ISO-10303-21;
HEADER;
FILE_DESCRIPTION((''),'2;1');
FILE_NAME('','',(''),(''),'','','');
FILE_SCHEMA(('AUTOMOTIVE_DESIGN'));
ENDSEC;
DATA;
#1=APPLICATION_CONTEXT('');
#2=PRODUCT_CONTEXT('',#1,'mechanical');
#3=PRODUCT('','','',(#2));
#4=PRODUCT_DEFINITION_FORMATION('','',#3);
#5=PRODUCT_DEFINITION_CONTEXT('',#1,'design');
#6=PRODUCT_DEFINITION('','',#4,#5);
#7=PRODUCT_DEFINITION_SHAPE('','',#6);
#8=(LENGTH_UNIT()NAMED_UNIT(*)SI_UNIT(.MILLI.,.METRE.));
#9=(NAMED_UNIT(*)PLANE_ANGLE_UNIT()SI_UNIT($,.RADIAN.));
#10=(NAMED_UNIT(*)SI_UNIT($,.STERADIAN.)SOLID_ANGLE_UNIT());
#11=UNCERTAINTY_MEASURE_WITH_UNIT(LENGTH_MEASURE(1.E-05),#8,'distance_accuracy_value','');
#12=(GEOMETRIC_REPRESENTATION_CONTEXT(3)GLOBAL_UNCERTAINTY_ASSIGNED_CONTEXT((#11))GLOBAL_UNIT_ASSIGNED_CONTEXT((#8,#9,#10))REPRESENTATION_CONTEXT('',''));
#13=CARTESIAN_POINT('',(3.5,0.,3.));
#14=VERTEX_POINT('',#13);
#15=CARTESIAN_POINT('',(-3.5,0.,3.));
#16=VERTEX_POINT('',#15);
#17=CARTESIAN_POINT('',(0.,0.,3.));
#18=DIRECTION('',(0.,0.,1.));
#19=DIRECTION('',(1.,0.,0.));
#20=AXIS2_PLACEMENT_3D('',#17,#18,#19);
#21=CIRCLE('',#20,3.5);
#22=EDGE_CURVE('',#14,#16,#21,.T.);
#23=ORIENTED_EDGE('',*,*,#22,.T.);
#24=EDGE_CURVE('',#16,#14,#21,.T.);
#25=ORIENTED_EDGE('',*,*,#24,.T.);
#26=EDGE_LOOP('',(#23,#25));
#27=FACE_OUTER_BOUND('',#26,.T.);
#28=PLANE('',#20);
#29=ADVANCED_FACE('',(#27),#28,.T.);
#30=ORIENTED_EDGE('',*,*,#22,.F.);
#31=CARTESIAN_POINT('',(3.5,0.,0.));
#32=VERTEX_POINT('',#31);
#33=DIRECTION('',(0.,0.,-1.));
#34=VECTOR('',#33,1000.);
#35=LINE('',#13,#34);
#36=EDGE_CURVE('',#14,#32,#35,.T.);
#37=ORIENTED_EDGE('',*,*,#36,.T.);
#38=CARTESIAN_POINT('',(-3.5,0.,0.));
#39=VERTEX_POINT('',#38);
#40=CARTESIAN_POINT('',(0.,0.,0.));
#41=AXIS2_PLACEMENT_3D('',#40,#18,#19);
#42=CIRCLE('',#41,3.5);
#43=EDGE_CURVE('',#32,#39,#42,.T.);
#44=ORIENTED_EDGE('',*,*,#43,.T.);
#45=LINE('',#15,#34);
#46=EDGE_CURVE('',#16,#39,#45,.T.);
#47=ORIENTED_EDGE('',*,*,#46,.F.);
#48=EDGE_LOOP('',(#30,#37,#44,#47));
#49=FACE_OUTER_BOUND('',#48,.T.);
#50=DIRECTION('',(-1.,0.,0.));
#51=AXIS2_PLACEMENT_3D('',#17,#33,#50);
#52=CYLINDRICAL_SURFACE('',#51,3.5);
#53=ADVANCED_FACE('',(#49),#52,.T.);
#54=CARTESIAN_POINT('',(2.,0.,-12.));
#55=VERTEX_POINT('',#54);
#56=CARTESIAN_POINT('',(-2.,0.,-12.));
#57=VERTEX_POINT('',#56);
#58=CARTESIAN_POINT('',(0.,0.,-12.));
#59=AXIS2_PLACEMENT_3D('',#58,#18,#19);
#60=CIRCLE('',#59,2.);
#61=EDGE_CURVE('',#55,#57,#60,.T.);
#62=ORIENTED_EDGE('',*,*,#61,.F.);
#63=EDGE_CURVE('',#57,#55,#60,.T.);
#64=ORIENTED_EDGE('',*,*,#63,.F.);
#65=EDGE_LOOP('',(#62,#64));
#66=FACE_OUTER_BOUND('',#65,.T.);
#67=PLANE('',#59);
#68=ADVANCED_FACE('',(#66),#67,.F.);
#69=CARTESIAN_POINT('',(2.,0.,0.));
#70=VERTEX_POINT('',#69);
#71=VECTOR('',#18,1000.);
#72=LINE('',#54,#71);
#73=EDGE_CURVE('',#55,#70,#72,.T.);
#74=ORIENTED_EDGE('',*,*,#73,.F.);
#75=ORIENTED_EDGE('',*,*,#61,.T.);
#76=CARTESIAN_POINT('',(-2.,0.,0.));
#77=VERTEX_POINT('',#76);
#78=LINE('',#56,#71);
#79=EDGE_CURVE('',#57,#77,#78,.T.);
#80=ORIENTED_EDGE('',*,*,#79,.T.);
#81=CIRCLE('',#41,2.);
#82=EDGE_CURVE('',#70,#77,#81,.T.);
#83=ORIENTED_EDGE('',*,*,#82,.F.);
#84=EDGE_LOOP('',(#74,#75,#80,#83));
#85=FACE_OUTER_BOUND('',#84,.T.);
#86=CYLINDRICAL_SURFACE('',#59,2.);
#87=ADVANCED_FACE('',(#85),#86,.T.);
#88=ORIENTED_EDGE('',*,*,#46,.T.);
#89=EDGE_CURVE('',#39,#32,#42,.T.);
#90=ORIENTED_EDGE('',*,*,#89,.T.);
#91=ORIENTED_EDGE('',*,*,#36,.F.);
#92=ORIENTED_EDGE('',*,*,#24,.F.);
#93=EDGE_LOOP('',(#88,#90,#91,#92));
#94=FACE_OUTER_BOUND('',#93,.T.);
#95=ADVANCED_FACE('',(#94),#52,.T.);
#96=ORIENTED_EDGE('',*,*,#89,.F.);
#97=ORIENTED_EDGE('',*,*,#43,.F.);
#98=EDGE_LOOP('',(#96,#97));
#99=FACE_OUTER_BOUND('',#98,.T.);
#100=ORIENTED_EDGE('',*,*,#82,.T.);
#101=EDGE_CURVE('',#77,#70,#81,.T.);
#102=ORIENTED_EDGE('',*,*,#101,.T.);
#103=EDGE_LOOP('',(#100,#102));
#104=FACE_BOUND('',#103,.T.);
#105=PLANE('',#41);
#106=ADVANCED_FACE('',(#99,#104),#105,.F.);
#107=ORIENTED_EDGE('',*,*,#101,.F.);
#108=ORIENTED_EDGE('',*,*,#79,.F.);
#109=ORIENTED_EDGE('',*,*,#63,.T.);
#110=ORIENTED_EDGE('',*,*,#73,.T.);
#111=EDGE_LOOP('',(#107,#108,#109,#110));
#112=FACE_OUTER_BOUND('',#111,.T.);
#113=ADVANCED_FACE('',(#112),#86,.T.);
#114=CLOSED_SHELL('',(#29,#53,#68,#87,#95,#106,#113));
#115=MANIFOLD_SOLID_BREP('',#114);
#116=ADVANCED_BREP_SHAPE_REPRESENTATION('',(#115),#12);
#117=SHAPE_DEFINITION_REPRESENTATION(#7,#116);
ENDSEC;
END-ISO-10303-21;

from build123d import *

# Parameters (mm, degrees)
SKETCH_1_R      = 2
EXTRUDE_1_DEPTH = 12
SKETCH_2_R      = 3.5
EXTRUDE_2_DEPTH = 3


with BuildPart() as part:
    # 草图1 → 凸台-拉伸1 (new body)
    with BuildSketch(Plane.XY):
        Circle(SKETCH_1_R)
    extrude(amount=-EXTRUDE_1_DEPTH)

    # 草图2 → 凸台-拉伸2 (add)
    with BuildSketch(Plane.XY):
        Circle(SKETCH_2_R)
    extrude(amount=EXTRUDE_2_DEPTH)


solid = part.part
